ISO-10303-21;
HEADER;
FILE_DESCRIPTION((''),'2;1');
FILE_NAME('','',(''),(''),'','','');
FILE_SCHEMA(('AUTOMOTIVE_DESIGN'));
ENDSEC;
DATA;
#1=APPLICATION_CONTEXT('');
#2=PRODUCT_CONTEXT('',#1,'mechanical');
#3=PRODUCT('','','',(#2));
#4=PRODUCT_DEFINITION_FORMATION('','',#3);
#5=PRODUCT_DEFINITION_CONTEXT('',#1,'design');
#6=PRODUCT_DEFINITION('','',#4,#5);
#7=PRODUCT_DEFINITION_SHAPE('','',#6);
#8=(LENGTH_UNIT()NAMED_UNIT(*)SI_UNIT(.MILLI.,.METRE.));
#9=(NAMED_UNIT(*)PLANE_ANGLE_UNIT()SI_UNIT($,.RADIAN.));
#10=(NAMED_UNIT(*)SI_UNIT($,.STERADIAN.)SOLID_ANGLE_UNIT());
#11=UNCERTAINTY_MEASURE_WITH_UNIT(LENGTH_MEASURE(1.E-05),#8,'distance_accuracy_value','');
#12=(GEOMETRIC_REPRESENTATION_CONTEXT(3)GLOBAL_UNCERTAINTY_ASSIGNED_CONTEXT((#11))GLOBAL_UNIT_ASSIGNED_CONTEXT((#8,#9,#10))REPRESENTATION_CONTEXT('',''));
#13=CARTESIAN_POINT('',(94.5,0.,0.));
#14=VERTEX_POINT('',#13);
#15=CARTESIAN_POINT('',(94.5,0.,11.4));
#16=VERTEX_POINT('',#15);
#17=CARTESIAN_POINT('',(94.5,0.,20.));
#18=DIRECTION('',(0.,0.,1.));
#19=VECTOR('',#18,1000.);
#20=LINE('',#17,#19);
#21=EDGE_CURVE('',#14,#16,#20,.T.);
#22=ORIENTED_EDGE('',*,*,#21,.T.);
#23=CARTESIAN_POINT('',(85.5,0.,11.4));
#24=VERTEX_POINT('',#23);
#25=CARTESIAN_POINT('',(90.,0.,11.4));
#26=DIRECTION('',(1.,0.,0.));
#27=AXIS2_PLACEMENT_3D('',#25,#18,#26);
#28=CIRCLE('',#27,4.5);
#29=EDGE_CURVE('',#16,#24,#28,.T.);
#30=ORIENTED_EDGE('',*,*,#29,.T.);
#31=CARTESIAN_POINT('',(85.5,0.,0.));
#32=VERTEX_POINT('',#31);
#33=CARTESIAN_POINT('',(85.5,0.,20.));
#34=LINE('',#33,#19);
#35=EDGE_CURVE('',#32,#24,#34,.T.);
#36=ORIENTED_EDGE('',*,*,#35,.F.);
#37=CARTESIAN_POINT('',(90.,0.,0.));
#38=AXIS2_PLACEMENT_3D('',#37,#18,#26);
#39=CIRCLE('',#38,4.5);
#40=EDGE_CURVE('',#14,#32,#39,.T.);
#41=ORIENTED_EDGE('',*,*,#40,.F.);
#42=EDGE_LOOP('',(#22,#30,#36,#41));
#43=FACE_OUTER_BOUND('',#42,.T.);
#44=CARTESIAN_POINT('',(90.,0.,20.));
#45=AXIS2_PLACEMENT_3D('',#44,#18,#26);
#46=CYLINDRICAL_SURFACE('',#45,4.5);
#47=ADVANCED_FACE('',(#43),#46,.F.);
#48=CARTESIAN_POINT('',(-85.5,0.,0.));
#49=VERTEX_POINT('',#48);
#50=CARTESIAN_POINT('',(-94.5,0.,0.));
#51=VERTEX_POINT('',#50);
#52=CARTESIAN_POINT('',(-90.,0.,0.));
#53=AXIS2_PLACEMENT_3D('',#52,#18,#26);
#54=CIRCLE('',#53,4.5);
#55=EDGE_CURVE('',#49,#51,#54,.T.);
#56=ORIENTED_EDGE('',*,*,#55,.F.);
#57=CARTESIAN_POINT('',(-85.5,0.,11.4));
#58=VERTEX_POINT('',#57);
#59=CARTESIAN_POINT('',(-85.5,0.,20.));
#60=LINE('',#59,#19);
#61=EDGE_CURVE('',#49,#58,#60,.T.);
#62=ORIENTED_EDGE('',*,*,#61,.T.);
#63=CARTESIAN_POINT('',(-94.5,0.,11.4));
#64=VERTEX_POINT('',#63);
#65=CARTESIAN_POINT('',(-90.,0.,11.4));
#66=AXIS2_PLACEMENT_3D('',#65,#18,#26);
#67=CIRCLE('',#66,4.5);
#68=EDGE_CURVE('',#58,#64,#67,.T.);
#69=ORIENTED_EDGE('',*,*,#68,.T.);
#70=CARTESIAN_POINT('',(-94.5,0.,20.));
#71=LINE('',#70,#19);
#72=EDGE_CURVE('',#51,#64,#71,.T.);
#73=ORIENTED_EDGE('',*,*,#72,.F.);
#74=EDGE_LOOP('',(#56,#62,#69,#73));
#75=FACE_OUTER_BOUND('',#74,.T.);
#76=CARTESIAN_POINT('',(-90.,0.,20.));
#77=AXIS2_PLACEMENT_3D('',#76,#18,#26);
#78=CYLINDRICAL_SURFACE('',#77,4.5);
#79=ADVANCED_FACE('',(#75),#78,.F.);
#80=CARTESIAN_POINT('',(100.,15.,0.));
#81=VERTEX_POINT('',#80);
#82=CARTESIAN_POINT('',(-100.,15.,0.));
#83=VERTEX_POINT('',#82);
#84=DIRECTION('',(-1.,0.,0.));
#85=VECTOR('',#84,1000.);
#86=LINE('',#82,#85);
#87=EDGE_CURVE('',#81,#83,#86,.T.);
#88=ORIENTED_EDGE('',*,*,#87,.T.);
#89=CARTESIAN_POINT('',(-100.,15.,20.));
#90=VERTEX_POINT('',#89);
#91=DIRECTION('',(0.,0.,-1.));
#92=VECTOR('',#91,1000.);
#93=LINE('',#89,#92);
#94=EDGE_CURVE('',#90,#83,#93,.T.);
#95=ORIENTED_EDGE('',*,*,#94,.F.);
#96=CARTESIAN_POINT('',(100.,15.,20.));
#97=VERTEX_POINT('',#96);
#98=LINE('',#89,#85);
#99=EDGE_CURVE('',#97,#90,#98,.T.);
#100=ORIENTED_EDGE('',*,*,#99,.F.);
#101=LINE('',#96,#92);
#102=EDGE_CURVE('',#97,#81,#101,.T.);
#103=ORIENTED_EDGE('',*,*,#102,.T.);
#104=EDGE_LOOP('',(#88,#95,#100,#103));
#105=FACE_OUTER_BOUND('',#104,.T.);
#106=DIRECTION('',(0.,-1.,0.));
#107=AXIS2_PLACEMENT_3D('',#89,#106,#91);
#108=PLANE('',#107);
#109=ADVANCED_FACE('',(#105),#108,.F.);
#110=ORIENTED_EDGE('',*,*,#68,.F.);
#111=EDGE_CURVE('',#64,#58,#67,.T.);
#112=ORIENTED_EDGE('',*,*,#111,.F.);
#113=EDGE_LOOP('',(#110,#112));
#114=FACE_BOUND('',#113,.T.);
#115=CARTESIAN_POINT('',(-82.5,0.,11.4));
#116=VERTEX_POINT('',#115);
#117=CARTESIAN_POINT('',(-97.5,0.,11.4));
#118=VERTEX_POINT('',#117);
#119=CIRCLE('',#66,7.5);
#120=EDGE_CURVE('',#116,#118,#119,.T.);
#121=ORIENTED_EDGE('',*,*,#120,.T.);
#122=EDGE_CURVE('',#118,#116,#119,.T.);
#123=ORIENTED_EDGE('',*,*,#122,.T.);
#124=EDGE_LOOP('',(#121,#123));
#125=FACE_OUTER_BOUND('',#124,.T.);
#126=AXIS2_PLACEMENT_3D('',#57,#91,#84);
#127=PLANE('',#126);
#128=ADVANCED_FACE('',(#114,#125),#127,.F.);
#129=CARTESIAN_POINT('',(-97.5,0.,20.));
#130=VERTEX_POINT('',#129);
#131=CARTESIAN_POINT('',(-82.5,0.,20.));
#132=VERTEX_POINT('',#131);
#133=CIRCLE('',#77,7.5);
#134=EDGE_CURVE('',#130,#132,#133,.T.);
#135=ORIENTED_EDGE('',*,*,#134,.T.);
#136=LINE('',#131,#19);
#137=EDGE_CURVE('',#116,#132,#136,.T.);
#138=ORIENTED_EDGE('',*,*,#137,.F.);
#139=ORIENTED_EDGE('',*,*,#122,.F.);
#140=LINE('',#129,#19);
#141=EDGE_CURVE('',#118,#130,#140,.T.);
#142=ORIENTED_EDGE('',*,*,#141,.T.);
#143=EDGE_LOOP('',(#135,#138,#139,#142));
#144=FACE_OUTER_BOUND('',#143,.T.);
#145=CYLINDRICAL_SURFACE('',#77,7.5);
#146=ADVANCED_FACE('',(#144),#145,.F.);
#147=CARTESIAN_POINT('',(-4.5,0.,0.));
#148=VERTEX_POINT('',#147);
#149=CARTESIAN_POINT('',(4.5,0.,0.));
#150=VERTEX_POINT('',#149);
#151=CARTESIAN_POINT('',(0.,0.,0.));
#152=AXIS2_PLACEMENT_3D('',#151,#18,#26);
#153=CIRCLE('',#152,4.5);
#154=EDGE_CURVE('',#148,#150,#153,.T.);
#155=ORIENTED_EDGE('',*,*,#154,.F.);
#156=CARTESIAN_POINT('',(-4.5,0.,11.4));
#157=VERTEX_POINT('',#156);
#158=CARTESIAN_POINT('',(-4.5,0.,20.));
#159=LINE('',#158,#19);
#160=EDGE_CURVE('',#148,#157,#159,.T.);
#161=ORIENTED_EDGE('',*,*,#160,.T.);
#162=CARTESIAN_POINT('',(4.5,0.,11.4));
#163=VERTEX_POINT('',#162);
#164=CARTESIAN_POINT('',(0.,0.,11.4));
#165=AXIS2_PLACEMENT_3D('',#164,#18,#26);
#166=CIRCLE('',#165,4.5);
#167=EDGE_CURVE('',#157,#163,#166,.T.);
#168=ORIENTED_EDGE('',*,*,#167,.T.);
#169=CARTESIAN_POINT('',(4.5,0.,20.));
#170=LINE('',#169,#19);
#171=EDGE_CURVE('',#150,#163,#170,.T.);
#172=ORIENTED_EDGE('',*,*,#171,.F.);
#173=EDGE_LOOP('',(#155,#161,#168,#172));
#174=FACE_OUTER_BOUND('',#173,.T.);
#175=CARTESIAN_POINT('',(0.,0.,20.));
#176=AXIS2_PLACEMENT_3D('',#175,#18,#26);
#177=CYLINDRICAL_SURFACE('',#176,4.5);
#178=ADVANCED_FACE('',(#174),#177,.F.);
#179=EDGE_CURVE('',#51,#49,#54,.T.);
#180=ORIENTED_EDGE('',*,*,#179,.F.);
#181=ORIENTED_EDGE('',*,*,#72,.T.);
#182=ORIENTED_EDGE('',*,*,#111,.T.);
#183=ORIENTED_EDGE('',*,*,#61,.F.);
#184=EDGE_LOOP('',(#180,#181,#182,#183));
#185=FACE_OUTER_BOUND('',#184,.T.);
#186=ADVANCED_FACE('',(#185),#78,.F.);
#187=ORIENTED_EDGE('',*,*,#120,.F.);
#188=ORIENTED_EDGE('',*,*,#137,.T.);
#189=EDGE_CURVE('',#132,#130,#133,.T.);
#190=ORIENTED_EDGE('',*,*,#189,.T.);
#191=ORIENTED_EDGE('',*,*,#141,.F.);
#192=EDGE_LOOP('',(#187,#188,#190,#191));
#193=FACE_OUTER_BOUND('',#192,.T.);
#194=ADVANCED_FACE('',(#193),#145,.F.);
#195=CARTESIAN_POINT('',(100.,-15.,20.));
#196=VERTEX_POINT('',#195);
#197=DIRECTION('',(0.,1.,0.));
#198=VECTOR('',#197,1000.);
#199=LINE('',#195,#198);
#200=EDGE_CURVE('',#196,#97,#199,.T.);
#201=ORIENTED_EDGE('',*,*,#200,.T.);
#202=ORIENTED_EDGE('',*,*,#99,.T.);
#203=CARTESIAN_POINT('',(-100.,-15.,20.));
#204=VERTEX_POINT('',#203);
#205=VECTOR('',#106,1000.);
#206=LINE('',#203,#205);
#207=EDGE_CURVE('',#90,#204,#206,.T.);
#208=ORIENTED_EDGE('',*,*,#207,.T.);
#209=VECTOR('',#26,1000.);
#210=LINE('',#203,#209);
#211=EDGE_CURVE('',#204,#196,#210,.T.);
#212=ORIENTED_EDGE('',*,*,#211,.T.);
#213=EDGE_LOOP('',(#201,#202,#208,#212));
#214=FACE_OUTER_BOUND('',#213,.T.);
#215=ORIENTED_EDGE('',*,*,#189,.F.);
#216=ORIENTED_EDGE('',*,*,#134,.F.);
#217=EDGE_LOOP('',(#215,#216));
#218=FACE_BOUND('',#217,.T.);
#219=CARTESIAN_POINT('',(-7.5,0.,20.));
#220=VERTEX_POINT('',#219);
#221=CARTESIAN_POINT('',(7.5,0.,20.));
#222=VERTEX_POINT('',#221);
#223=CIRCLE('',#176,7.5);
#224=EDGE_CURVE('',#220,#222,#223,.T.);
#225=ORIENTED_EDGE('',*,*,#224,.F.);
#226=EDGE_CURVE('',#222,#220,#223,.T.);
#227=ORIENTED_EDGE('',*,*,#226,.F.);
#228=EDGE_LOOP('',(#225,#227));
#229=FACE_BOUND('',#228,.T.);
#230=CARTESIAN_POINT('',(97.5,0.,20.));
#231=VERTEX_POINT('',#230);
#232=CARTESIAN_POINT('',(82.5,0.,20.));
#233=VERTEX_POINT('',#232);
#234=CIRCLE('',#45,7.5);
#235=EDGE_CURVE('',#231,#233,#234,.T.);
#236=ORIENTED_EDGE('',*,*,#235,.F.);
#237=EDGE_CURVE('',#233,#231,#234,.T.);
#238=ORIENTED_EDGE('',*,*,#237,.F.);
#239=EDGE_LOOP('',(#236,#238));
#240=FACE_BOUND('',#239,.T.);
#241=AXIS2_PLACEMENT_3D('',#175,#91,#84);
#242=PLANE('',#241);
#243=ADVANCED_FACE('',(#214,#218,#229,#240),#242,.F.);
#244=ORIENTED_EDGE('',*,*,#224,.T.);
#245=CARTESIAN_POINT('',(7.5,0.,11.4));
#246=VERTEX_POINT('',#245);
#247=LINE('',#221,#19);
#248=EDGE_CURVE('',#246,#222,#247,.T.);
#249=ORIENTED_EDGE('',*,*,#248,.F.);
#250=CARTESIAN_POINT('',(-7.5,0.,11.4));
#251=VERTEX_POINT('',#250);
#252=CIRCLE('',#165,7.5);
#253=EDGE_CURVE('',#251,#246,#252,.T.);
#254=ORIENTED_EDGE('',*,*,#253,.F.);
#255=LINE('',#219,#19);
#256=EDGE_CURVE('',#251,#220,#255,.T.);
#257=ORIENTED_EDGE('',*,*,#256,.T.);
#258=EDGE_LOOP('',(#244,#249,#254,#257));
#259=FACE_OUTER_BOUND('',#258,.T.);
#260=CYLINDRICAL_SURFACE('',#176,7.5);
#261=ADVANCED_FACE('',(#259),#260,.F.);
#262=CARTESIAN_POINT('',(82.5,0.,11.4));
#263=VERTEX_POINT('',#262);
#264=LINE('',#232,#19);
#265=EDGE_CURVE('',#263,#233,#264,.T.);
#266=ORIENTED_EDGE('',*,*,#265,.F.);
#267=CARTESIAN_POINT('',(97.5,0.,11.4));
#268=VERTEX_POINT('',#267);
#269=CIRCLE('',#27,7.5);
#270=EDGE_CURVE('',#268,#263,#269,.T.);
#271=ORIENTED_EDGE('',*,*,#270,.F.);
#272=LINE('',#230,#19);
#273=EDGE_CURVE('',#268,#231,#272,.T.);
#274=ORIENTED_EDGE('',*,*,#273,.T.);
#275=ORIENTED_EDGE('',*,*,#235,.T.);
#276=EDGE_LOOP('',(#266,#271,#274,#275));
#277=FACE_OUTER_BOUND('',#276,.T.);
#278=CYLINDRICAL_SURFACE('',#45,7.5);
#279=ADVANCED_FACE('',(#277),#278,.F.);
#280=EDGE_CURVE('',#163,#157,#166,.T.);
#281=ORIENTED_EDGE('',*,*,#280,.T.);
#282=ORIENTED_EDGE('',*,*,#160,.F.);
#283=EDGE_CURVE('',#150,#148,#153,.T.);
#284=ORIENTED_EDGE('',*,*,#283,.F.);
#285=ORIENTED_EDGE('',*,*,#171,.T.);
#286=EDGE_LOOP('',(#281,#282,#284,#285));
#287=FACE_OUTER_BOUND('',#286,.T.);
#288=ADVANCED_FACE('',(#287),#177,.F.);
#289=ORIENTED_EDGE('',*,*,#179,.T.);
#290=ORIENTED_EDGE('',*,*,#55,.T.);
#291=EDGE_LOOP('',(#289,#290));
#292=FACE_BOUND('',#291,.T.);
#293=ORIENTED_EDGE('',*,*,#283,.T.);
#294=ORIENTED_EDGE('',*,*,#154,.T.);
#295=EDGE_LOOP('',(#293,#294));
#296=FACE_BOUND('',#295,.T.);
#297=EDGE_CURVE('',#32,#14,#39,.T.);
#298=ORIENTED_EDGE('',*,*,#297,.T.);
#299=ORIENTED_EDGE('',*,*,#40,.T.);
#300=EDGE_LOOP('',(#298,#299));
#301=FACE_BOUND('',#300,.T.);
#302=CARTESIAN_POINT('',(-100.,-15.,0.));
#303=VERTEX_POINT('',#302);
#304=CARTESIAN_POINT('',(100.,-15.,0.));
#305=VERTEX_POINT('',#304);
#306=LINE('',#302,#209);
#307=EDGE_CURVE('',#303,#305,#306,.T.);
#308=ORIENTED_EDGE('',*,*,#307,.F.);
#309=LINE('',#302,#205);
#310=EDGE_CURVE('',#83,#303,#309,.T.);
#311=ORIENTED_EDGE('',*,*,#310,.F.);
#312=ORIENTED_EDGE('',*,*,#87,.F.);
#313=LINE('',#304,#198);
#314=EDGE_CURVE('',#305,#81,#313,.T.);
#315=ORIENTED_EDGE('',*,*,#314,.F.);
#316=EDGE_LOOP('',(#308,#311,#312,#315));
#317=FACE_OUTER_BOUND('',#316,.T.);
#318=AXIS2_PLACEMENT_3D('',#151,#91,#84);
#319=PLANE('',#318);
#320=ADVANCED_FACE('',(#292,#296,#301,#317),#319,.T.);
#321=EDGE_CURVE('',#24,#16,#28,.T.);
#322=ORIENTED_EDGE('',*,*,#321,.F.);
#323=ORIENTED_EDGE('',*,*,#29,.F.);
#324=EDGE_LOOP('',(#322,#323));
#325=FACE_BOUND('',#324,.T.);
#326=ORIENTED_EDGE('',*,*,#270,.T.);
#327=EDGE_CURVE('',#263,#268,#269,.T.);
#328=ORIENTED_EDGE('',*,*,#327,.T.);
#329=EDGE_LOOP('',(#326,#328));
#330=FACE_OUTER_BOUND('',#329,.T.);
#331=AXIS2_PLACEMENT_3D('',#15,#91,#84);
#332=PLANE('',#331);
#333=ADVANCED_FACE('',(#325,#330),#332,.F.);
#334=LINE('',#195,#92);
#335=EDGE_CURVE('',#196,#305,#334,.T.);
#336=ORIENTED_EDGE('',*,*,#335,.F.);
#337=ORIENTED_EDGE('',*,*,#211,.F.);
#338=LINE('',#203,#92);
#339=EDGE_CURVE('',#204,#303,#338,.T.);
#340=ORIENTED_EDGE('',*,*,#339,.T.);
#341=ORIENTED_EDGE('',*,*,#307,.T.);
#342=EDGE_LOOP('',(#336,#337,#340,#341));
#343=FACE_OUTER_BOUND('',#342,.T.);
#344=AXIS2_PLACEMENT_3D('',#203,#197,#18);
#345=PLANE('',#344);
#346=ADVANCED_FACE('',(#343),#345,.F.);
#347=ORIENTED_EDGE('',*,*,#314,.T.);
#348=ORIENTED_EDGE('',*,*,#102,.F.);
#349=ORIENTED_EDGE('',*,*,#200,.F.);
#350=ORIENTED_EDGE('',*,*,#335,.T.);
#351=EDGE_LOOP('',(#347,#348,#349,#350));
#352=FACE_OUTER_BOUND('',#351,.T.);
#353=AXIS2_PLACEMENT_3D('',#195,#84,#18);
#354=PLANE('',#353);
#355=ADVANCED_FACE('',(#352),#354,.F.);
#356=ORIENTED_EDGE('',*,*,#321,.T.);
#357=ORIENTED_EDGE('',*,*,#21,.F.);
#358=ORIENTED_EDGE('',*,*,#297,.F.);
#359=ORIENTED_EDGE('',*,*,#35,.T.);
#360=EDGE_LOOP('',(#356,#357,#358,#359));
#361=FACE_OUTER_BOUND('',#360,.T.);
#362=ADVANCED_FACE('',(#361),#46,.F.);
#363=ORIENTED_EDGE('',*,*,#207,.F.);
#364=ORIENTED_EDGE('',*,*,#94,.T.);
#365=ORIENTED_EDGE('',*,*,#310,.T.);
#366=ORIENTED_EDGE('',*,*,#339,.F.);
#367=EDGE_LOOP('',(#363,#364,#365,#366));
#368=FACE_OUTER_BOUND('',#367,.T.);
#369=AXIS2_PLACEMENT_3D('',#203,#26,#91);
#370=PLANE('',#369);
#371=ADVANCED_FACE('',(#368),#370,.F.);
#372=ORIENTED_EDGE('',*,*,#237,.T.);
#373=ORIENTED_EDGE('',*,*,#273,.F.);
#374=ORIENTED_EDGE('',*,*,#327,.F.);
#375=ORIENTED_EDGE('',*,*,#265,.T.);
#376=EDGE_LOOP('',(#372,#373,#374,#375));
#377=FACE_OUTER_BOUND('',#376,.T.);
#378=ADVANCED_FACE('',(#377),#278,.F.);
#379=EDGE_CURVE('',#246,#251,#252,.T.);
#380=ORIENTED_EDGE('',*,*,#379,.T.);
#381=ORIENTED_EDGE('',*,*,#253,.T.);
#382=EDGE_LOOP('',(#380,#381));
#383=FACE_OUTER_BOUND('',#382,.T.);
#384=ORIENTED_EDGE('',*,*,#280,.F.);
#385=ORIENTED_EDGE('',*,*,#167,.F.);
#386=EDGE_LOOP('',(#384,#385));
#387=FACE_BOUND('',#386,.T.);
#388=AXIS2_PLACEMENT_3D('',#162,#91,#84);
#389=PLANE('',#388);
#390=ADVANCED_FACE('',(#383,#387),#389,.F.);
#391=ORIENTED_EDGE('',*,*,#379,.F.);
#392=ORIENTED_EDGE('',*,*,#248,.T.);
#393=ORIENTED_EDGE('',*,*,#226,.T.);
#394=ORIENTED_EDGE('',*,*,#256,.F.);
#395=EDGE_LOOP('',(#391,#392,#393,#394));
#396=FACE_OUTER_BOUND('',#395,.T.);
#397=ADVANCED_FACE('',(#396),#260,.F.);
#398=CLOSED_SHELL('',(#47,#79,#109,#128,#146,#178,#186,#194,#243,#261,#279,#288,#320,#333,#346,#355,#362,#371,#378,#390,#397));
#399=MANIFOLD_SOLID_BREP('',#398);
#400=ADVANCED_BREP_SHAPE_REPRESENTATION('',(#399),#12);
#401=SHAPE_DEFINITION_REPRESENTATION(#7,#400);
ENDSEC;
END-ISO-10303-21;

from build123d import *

# Parameters (mm, degrees)
SKETCH_1_W                   = 200
SKETCH_1_H                   = 30
EXTRUDE_1_DEPTH              = 20
HOLE_WIZARD_M8_1_D           = 9
HOLE_WIZARD_M8_1_CBORE_D     = 15
HOLE_WIZARD_M8_1_CBORE_DEPTH = 8.6


with BuildPart() as part:
    # 草图1 → 凸台-拉伸1 (new body)
    with BuildSketch(Plane.XY):
        Rectangle(SKETCH_1_W, SKETCH_1_H)
    extrude(amount=EXTRUDE_1_DEPTH)

    # M8 六角凹头螺钉的柱形沉头孔1 (through all)
    with Locations(Plane.XY.offset(20)):
        with Locations((0, 0), (90, 0), (-90, 0)):
            CounterBoreHole(HOLE_WIZARD_M8_1_D / 2, HOLE_WIZARD_M8_1_CBORE_D / 2, HOLE_WIZARD_M8_1_CBORE_DEPTH)


solid = part.part
